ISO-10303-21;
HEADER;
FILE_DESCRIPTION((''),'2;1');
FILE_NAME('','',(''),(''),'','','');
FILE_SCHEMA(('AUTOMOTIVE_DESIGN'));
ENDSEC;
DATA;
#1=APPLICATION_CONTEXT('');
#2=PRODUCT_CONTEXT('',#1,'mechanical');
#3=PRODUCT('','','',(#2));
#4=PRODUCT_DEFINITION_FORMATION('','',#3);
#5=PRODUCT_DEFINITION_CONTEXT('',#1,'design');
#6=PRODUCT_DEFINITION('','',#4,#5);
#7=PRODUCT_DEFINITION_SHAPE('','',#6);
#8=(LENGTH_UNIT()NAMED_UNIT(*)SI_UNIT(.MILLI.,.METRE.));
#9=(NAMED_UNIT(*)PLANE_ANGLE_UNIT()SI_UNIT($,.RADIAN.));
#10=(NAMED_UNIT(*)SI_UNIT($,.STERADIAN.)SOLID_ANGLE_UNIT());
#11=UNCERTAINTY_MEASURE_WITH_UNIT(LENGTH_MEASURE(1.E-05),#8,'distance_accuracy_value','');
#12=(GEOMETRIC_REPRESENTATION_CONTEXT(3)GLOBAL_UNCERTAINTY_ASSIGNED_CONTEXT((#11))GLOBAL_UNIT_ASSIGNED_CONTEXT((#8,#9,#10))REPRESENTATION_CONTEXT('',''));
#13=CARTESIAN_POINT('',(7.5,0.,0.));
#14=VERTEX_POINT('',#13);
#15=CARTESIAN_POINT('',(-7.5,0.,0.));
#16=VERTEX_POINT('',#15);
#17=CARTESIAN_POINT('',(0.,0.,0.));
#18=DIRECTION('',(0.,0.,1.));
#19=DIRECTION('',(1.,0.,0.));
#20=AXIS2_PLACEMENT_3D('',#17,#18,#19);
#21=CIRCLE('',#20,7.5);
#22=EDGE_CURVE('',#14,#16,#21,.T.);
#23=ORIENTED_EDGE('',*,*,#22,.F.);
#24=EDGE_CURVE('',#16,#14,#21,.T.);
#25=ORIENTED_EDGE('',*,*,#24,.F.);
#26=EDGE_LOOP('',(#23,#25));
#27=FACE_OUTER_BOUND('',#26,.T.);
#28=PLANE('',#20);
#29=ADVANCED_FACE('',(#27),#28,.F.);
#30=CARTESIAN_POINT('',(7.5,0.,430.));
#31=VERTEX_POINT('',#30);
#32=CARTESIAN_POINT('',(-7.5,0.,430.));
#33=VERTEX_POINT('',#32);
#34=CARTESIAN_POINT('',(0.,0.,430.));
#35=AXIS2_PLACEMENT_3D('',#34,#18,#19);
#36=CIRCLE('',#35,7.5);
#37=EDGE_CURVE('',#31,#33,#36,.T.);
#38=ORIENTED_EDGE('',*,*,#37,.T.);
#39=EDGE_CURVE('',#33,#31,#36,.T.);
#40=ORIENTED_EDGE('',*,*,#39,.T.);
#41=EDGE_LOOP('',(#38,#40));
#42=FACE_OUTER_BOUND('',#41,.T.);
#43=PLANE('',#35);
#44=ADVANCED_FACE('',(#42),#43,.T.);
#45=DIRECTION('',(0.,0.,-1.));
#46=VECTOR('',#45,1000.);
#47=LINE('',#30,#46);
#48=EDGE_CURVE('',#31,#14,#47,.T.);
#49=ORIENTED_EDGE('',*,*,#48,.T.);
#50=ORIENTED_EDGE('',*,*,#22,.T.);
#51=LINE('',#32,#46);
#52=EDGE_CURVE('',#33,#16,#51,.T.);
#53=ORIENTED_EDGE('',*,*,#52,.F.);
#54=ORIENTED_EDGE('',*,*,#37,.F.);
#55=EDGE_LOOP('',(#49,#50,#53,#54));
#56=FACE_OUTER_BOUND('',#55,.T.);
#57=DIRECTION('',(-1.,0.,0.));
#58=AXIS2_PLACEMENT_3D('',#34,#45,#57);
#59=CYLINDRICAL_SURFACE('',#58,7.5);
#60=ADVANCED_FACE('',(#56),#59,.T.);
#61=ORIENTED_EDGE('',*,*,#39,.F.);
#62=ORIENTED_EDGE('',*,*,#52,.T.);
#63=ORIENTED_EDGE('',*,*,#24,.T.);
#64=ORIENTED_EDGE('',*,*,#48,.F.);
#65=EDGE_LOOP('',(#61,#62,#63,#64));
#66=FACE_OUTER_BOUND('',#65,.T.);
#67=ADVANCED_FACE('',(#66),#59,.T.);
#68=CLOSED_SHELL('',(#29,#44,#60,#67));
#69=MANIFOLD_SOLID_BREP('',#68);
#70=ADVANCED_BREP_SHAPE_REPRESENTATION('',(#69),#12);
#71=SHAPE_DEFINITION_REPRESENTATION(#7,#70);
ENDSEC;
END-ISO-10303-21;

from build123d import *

# Parameters (mm, degrees)
SKETCH_1_R      = 7.5
EXTRUDE_1_DEPTH = 430


with BuildPart() as part:
    # 草图1 → 凸台-拉伸1 (new body)
    with BuildSketch(Plane.XY):
        Circle(SKETCH_1_R)
    extrude(amount=EXTRUDE_1_DEPTH)


solid = part.part
